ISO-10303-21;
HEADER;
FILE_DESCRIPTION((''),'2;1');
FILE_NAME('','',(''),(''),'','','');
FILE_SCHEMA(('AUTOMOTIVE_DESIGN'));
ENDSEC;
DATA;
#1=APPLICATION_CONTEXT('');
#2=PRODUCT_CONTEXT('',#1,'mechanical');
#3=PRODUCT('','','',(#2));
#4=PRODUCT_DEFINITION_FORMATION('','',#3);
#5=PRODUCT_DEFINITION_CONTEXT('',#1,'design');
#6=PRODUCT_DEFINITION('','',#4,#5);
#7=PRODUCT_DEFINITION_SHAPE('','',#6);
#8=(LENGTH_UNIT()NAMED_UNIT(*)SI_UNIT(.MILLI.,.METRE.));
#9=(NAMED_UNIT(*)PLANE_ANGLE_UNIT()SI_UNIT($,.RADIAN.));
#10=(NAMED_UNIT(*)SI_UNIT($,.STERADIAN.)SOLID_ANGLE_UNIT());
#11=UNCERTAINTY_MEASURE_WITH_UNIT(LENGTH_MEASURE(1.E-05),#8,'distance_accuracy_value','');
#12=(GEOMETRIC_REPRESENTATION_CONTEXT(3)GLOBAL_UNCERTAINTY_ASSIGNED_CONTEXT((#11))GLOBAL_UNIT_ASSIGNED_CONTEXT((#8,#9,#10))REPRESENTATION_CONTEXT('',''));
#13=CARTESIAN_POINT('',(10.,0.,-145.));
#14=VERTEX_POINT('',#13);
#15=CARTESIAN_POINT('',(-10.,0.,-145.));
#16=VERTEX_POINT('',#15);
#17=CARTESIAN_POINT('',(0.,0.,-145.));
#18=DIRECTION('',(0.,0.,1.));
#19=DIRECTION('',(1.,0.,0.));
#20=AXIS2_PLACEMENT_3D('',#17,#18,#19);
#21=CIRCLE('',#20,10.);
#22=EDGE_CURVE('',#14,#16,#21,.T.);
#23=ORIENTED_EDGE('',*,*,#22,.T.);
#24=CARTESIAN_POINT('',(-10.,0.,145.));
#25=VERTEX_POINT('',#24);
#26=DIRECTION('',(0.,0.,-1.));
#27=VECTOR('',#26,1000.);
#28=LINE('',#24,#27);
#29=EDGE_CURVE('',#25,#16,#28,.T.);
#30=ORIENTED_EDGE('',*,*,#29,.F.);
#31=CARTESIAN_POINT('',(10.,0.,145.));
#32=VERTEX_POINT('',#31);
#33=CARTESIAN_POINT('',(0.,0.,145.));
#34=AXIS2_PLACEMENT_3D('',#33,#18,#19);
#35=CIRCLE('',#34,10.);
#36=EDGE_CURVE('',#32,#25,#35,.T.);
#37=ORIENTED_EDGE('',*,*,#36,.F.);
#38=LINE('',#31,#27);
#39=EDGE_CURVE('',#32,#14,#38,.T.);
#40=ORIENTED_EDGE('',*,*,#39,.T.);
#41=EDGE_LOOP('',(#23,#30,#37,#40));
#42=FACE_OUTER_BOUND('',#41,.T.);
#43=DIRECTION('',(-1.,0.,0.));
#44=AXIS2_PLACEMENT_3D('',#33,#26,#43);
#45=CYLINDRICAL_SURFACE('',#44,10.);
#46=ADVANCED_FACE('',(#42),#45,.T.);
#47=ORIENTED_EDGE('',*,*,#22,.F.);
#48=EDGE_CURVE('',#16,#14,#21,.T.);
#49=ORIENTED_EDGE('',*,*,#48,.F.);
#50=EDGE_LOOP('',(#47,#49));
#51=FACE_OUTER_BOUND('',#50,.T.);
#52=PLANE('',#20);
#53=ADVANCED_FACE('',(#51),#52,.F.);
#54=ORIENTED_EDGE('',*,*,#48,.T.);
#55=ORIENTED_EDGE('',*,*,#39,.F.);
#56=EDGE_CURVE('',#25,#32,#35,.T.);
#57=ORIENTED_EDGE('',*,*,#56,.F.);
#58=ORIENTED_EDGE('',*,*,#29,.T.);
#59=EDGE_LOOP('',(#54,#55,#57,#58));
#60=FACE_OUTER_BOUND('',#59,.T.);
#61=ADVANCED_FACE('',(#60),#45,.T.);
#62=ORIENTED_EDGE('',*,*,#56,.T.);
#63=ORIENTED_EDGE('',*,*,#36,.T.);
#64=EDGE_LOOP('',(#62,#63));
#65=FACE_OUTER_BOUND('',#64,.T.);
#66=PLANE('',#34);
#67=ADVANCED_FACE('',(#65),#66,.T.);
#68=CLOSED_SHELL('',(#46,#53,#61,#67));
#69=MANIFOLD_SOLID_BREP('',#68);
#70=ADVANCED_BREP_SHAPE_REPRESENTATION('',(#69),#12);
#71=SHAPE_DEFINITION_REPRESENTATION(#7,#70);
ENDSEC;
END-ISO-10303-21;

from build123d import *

# Parameters (mm, degrees)
SKETCH_1_R      = 10
EXTRUDE_1_DEPTH = 145


with BuildPart() as part:
    # 草图1 → 凸台-拉伸1 (new, symmetric)
    with BuildSketch(Plane.XY):
        Circle(SKETCH_1_R)
    extrude(amount=EXTRUDE_1_DEPTH, both=True)


solid = part.part
